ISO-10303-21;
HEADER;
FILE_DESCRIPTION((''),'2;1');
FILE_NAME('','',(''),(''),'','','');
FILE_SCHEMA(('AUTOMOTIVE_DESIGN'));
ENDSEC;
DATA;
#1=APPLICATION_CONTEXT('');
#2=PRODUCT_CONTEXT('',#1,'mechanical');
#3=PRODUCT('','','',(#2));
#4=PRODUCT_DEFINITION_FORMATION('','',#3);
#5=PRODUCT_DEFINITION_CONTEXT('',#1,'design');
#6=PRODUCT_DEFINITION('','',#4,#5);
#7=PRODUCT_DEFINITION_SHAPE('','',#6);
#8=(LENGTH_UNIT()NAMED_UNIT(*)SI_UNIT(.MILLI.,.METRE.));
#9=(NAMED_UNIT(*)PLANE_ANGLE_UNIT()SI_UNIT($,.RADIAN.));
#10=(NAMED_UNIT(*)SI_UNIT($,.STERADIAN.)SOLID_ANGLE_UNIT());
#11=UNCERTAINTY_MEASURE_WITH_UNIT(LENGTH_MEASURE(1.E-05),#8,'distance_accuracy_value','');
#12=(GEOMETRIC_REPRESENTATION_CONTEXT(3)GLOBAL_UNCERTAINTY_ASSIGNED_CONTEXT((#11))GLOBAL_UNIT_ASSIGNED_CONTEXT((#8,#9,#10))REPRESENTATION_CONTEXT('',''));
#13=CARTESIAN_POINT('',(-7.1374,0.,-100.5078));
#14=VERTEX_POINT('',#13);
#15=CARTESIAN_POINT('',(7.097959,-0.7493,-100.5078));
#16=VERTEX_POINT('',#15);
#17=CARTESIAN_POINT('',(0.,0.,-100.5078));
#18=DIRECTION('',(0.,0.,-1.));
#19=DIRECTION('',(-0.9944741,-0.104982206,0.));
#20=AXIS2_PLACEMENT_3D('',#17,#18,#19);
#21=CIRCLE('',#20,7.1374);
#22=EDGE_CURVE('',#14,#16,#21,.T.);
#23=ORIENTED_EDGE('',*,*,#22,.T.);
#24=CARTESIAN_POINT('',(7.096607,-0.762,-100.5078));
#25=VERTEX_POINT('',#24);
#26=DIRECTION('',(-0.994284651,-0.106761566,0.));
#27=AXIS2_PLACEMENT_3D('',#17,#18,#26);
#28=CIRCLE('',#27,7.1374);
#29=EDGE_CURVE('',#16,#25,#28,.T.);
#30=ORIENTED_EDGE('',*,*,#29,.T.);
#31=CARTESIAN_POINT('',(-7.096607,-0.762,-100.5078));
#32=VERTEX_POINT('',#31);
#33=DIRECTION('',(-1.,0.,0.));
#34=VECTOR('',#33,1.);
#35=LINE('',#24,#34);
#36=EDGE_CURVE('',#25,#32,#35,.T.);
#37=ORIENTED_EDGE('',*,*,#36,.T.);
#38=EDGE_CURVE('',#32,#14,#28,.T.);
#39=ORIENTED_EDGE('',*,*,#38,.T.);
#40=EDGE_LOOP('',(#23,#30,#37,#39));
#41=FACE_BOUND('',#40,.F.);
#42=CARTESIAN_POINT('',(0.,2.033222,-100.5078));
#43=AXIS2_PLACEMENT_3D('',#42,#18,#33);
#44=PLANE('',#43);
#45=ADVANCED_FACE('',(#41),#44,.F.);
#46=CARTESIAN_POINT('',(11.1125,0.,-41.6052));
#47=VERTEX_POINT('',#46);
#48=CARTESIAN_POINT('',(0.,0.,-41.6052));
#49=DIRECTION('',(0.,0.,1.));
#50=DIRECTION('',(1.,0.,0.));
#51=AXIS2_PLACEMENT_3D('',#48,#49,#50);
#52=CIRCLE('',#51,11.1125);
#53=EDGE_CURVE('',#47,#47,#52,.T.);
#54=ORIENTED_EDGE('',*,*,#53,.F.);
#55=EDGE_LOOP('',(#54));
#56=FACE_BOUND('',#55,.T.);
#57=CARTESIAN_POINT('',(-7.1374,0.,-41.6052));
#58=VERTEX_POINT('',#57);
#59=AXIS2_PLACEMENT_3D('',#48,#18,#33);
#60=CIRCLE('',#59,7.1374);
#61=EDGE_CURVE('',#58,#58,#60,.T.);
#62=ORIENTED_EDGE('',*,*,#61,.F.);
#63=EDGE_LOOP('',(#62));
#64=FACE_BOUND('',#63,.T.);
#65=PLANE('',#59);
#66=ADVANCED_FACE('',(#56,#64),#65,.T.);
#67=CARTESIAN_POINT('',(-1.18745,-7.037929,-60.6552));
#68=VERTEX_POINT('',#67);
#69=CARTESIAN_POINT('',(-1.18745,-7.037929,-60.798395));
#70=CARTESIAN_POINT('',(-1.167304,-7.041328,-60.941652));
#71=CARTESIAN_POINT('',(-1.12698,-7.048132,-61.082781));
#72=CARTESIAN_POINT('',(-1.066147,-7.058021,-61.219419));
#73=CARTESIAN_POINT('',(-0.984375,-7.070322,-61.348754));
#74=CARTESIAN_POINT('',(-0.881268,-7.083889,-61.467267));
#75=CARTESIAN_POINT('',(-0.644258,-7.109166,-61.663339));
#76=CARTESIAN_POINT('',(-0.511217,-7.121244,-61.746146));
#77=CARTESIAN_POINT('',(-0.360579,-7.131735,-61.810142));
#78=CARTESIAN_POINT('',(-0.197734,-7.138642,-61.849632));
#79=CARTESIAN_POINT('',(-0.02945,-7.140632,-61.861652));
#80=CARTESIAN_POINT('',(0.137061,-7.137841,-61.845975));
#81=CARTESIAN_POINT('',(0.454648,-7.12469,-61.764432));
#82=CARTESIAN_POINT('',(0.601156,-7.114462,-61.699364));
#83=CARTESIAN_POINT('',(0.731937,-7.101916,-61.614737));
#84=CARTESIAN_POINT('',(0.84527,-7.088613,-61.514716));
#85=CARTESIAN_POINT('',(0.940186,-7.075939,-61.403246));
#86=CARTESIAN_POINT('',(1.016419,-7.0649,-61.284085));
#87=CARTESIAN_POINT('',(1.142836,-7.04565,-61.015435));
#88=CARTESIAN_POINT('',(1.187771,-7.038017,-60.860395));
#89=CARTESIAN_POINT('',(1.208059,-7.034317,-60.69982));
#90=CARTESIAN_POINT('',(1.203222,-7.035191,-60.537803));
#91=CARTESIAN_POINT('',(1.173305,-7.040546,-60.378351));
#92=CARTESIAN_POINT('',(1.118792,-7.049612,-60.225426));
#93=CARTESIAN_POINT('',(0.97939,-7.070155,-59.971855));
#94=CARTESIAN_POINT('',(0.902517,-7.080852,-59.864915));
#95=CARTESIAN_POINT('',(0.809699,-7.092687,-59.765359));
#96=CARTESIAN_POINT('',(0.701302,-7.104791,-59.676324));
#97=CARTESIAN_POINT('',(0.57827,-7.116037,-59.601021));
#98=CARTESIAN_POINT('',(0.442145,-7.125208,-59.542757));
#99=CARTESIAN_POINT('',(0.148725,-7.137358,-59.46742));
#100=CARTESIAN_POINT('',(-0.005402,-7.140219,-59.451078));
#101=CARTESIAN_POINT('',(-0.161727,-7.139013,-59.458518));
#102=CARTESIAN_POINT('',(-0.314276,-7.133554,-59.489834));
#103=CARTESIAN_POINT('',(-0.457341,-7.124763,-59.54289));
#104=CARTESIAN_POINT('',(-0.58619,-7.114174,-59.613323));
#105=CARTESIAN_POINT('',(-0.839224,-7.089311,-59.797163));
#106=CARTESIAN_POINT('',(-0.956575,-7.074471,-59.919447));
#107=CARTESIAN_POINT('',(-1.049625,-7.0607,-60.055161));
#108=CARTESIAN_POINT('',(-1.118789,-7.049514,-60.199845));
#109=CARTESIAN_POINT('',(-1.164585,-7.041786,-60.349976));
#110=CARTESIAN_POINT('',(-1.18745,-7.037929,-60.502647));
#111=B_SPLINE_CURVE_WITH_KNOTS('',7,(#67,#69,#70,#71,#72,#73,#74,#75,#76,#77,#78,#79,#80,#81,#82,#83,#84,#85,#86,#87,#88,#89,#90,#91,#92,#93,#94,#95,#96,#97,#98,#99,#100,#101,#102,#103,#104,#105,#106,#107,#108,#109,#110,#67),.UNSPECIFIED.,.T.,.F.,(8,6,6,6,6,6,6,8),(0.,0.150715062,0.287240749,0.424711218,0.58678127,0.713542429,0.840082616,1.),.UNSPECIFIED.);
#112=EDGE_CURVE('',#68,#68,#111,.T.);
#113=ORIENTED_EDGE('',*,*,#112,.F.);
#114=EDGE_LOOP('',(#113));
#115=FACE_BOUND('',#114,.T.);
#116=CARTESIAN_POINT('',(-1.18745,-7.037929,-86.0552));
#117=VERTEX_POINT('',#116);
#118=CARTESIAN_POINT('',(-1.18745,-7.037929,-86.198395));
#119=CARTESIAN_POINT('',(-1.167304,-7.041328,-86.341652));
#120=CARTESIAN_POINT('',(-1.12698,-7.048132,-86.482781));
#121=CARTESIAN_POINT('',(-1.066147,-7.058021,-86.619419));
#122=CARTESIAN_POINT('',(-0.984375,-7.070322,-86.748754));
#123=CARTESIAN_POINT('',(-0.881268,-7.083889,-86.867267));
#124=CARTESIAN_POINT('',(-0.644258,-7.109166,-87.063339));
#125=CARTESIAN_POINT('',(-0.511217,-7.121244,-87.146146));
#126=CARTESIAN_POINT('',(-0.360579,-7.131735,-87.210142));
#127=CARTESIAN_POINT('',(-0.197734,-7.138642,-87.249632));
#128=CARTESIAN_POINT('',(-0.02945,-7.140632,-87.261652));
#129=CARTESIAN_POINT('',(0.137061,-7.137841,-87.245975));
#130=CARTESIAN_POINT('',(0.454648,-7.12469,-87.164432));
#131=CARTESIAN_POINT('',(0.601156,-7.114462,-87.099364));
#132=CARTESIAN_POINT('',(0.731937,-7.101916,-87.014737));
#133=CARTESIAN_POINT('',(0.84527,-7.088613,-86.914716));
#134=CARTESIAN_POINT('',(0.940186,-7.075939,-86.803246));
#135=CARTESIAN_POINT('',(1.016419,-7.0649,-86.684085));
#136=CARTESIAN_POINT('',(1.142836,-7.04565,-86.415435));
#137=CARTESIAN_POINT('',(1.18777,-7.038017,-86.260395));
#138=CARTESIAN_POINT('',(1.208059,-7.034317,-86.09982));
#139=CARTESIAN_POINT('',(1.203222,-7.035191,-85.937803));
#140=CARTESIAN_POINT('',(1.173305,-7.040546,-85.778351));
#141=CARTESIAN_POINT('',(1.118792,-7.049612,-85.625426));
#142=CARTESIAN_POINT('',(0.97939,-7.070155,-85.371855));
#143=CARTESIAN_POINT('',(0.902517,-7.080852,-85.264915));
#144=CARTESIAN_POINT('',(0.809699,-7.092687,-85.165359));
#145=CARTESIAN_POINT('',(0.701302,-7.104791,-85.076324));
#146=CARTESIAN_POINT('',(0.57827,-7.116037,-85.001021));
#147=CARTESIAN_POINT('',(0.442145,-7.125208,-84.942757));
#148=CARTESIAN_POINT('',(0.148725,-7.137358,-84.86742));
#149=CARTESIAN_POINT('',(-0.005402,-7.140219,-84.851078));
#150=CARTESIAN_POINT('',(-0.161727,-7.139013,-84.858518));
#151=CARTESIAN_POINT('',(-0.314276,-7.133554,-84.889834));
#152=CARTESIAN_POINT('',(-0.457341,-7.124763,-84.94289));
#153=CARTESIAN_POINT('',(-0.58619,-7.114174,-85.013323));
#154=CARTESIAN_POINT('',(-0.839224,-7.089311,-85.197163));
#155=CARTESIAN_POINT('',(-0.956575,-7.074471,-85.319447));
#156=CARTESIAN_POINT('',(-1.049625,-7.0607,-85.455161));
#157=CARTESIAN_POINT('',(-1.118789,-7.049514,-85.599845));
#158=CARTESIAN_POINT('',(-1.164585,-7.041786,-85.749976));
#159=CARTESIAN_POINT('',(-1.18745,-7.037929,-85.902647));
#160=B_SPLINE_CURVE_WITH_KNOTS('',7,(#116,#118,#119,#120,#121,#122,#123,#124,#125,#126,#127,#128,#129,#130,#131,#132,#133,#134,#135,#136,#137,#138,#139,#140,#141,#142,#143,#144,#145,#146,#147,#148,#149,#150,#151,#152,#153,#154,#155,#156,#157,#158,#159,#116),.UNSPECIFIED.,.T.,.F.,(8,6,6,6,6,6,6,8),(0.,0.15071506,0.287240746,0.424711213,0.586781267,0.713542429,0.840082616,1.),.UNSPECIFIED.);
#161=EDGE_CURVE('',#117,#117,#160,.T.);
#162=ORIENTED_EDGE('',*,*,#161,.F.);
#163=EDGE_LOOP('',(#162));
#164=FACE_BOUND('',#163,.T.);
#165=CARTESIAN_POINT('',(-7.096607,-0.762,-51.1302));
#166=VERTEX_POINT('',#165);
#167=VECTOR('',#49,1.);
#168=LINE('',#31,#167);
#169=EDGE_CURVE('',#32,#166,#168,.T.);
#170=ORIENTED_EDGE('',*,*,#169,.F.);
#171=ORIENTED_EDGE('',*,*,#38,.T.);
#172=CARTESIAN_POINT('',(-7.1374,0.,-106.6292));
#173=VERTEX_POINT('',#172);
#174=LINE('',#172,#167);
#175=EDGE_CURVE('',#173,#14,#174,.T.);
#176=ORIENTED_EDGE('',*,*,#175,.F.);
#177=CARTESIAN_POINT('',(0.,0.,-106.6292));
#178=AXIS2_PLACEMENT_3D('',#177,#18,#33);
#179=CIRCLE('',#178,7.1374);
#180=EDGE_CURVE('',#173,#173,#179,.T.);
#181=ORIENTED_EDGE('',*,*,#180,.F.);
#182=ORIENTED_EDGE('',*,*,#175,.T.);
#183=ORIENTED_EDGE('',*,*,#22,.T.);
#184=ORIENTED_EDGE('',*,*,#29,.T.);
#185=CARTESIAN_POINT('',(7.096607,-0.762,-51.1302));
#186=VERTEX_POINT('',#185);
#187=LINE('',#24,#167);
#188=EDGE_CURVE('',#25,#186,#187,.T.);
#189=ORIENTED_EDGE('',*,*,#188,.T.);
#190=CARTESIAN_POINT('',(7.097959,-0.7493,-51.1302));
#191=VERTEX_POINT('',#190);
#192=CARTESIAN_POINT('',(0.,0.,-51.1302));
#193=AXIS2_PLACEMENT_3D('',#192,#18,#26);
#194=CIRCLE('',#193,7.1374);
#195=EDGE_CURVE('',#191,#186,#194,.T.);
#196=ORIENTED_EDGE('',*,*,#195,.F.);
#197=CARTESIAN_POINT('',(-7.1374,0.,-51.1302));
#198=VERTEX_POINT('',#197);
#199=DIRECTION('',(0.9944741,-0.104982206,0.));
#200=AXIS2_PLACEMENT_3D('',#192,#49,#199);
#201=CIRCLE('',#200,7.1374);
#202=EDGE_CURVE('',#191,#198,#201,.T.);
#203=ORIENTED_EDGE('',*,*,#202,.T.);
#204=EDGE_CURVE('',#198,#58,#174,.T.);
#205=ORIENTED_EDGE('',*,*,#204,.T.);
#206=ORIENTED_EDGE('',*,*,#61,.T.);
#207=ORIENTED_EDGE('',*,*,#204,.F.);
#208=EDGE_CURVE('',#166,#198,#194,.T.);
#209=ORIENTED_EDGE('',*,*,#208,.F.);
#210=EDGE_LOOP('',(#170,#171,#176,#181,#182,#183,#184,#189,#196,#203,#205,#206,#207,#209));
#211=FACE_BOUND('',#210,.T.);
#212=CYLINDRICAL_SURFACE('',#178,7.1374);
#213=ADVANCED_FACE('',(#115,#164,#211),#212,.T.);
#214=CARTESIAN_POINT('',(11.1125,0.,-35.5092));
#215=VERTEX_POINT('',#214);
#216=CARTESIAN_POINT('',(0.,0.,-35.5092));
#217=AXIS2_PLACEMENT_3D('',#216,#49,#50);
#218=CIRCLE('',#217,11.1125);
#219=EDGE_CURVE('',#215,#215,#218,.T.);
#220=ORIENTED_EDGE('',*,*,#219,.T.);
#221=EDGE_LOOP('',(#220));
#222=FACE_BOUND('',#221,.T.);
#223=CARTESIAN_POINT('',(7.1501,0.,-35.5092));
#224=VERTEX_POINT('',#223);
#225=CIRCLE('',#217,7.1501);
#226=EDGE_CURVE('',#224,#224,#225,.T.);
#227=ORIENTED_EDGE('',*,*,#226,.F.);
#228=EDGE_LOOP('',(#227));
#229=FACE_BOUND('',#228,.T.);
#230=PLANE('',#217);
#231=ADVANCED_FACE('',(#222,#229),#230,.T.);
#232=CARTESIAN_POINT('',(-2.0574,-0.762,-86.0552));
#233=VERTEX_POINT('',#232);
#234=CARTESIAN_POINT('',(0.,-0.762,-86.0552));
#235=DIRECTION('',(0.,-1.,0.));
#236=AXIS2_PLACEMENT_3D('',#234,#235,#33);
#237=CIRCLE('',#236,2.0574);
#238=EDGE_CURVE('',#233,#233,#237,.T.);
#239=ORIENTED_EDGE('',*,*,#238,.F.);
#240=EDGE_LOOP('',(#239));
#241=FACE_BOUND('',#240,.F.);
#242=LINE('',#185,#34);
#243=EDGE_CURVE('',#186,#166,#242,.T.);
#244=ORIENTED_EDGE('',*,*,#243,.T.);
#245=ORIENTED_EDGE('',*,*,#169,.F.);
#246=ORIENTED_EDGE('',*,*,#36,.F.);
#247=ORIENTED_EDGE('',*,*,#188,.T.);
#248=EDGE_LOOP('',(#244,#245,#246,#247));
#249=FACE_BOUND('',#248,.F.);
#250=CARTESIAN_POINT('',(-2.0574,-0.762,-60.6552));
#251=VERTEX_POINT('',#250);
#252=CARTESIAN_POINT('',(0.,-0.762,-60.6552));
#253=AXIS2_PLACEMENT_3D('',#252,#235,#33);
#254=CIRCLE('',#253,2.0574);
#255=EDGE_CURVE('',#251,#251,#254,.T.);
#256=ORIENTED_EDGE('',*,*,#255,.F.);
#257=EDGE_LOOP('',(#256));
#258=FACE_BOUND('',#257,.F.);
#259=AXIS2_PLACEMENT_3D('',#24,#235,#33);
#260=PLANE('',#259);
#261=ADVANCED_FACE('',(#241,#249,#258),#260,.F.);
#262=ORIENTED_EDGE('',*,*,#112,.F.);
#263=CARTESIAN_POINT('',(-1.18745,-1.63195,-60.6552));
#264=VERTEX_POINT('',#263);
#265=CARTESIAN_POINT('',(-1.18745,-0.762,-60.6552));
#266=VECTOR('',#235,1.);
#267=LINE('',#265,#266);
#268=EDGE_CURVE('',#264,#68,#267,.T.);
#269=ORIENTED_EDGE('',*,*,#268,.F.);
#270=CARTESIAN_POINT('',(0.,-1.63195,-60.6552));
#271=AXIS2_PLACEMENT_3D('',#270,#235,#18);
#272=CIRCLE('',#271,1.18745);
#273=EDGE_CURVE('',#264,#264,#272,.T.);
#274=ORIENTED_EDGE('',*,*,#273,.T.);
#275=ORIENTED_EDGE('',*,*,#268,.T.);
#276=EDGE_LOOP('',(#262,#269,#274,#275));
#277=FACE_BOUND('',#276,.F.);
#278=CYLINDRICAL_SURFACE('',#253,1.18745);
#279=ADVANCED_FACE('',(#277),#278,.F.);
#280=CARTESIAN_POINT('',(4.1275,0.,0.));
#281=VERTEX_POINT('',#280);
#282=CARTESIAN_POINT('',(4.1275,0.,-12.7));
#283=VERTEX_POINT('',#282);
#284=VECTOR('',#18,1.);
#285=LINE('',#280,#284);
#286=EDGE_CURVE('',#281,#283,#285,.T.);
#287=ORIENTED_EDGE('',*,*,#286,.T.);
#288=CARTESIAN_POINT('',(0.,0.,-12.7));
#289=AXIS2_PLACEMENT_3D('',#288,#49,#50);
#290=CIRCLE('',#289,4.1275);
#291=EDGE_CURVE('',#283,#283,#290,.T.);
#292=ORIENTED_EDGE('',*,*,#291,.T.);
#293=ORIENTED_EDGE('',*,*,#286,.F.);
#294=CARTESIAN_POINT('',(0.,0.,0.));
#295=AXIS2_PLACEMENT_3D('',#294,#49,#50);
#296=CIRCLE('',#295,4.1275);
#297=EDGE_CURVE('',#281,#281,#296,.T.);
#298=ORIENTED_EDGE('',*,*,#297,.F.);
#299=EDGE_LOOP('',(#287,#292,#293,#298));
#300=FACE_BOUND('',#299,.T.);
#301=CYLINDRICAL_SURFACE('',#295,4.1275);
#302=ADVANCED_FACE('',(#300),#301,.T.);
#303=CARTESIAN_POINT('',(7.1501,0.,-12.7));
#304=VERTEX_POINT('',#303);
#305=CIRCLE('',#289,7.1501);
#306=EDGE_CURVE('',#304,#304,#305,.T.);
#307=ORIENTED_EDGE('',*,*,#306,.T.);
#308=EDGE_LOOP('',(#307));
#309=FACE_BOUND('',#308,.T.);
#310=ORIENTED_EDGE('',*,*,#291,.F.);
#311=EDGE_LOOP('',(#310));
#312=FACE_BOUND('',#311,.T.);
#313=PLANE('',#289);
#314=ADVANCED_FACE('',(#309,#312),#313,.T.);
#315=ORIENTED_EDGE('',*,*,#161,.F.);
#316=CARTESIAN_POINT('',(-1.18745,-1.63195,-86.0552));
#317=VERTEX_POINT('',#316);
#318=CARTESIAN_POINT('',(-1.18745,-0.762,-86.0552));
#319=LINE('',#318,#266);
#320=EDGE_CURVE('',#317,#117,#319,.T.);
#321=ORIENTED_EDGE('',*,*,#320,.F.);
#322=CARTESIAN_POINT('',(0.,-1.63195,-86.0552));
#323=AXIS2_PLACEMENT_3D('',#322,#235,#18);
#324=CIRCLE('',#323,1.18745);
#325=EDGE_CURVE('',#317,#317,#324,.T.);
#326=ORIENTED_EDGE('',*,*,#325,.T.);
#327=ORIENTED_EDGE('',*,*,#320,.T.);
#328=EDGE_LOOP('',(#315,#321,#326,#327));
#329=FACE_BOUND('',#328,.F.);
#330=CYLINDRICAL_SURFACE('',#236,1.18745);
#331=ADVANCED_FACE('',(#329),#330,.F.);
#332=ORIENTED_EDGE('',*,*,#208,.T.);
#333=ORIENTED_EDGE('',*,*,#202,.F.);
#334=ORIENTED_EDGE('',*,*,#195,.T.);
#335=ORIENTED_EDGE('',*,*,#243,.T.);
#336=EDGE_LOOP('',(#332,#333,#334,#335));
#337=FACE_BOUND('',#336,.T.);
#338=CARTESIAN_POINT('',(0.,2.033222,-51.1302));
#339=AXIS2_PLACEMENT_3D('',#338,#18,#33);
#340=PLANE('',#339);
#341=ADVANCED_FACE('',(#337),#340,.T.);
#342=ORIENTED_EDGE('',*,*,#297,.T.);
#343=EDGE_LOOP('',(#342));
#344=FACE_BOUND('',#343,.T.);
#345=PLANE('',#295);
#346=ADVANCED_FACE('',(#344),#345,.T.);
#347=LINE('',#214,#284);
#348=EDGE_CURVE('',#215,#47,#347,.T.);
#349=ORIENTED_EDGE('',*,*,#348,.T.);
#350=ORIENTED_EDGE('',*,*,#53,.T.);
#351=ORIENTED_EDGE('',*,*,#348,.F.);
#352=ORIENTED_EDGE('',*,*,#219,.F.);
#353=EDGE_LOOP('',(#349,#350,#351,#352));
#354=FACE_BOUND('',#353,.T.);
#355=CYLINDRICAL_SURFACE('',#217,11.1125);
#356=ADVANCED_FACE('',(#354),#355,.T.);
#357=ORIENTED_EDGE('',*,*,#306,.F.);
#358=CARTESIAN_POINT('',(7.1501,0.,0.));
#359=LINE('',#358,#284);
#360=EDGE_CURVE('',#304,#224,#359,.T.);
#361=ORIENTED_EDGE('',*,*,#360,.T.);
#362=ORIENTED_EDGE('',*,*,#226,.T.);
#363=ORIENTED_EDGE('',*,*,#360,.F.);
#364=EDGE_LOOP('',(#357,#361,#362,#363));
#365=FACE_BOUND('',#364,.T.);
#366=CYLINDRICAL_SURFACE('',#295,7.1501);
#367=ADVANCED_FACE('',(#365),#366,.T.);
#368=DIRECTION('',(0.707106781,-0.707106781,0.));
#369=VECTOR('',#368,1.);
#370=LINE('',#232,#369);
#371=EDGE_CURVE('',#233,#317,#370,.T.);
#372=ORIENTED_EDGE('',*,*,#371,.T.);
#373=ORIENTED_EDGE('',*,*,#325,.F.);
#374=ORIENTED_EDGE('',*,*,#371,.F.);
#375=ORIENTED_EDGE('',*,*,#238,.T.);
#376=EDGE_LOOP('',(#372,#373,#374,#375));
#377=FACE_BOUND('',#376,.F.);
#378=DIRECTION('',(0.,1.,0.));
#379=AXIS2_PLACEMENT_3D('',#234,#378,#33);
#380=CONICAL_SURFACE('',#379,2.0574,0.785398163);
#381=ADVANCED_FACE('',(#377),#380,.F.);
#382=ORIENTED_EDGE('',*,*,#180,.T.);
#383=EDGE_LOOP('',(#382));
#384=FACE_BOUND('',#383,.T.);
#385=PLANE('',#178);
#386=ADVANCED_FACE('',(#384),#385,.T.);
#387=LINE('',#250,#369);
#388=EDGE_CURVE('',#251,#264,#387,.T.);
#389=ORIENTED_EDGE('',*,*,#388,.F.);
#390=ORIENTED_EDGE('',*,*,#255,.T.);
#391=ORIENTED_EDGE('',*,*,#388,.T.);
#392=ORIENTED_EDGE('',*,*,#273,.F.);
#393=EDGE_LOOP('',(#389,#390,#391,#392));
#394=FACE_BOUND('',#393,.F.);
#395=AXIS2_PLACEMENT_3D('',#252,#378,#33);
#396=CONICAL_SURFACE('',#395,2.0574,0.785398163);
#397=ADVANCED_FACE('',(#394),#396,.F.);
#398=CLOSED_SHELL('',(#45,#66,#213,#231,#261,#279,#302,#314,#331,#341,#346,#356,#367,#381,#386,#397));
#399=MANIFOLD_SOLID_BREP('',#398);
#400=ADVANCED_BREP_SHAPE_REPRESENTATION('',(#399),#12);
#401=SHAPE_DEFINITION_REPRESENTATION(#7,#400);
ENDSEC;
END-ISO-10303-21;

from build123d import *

# Parameters (mm, degrees)
SKETCH2_R                       = 7.1501
BOSS_EXTRUDE1_DEPTH             = 106.6292
SKETCH9_R                       = 11.1125
BOSS_EXTRUDE3_DEPTH             = 6.096
CUT_EXTRUDE1_DEPTH              = 49.3776
F_4_48_TAPPED_HOLE1_D           = 2.3749
F_4_48_TAPPED_HOLE1_CSINK_D     = 4.1148
F_4_48_TAPPED_HOLE1_CSINK_ANGLE = 90
SKETCH15_R                      = 7.1374
BOSS_EXTRUDE4_DEPTH             = 65.024
SKETCH16_OUTSIDE_W              = 46.46
SKETCH16_OUTSIDE_H              = 46.46
SKETCH16_OUTSIDE_R              = 7.1374
CUT_EXTRUDE2_DEPTH              = 65.024
CUT_EXTRUDE3_START              = 49.3776
CUT_EXTRUDE3_DEPTH              = 49.3776
SKETCH19_OUTSIDE_W              = 46.46
SKETCH19_OUTSIDE_H              = 46.46
SKETCH19_OUTSIDE_R              = 4.1275
CUT_EXTRUDE4_DEPTH              = 12.7
F_4_48_TAPPED_HOLE2_D           = 2.3749
F_4_48_TAPPED_HOLE2_CSINK_D     = 4.1148
F_4_48_TAPPED_HOLE2_CSINK_ANGLE = 90


with BuildPart() as part:
    # Sketch2 → Boss-Extrude1 (new body)
    with BuildSketch(Plane.XY):
        Circle(SKETCH2_R)
    extrude(amount=-BOSS_EXTRUDE1_DEPTH)

    # Sketch9 → Boss-Extrude3 (add)
    with BuildSketch(Plane.XY.offset(-35.5092)):
        Circle(SKETCH9_R)
    extrude(amount=-BOSS_EXTRUDE3_DEPTH)

    # Sketch11 → Cut-Extrude1 (cut)
    with BuildSketch(Plane(origin=(0, 0, -51.1302), x_dir=(-1, 0, 0), z_dir=(0, 0, -1))):
        with BuildLine():
            Line((-7.110729887, -0.7493), (7.110729887, -0.7493))
            ThreePointArc((7.110729887, -0.7493), (0, 7.1501), (-7.110729887, -0.7493))
        make_face()
    extrude(amount=CUT_EXTRUDE1_DEPTH, mode=Mode.SUBTRACT)

    # #4-48 Tapped Hole1 (through all)
    with Locations(Plane(origin=(0, -0.7493, 0), x_dir=(1, 0, 0), z_dir=(0, 1, 0))):
        with Locations((0, 86.0552), (0, 60.6552)):
            CounterSinkHole(F_4_48_TAPPED_HOLE1_D / 2, F_4_48_TAPPED_HOLE1_CSINK_D / 2, counter_sink_angle=F_4_48_TAPPED_HOLE1_CSINK_ANGLE)

    # Sketch15 → Boss-Extrude4 (add)
    with BuildSketch(Plane(origin=(0, 0, -106.6292), x_dir=(-1, 0, 0), z_dir=(0, 0, -1))):
        Circle(SKETCH15_R)
    extrude(amount=-BOSS_EXTRUDE4_DEPTH)

    # Sketch16 outside → Cut-Extrude2 (cut)
    with BuildSketch(Plane(origin=(0, 0, -106.6292), x_dir=(-1, 0, 0), z_dir=(0, 0, -1))):
        Rectangle(SKETCH16_OUTSIDE_W, SKETCH16_OUTSIDE_H)
        Circle(SKETCH16_OUTSIDE_R, mode=Mode.SUBTRACT)
    extrude(amount=-CUT_EXTRUDE2_DEPTH, mode=Mode.SUBTRACT)

    # Sketch18 → Cut-Extrude3 (cut)
    with BuildSketch(Plane(origin=(0, 0, -51.1302), x_dir=(-1, 0, 0), z_dir=(0, 0, -1)).offset(CUT_EXTRUDE3_START)):
        with BuildLine():
            Line((-7.096607271, -0.762), (7.096607271, -0.762))
            ThreePointArc((7.096607271, -0.762), (0, 7.1374), (-7.096607271, -0.762))
        make_face()
    extrude(amount=-CUT_EXTRUDE3_DEPTH, mode=Mode.SUBTRACT)

    # Sketch19 outside → Cut-Extrude4 (cut)
    with BuildSketch(Plane.XY):
        Rectangle(SKETCH19_OUTSIDE_W, SKETCH19_OUTSIDE_H)
        Circle(SKETCH19_OUTSIDE_R, mode=Mode.SUBTRACT)
    extrude(amount=-CUT_EXTRUDE4_DEPTH, mode=Mode.SUBTRACT)

    # #4-48 Tapped Hole2 (through all)
    with Locations(Plane(origin=(0, -0.762, 0), x_dir=(1, 0, 0), z_dir=(0, 1, 0))):
        with Locations((0, 60.6552), (0, 86.0552)):
            CounterSinkHole(F_4_48_TAPPED_HOLE2_D / 2, F_4_48_TAPPED_HOLE2_CSINK_D / 2, counter_sink_angle=F_4_48_TAPPED_HOLE2_CSINK_ANGLE)


solid = part.part
